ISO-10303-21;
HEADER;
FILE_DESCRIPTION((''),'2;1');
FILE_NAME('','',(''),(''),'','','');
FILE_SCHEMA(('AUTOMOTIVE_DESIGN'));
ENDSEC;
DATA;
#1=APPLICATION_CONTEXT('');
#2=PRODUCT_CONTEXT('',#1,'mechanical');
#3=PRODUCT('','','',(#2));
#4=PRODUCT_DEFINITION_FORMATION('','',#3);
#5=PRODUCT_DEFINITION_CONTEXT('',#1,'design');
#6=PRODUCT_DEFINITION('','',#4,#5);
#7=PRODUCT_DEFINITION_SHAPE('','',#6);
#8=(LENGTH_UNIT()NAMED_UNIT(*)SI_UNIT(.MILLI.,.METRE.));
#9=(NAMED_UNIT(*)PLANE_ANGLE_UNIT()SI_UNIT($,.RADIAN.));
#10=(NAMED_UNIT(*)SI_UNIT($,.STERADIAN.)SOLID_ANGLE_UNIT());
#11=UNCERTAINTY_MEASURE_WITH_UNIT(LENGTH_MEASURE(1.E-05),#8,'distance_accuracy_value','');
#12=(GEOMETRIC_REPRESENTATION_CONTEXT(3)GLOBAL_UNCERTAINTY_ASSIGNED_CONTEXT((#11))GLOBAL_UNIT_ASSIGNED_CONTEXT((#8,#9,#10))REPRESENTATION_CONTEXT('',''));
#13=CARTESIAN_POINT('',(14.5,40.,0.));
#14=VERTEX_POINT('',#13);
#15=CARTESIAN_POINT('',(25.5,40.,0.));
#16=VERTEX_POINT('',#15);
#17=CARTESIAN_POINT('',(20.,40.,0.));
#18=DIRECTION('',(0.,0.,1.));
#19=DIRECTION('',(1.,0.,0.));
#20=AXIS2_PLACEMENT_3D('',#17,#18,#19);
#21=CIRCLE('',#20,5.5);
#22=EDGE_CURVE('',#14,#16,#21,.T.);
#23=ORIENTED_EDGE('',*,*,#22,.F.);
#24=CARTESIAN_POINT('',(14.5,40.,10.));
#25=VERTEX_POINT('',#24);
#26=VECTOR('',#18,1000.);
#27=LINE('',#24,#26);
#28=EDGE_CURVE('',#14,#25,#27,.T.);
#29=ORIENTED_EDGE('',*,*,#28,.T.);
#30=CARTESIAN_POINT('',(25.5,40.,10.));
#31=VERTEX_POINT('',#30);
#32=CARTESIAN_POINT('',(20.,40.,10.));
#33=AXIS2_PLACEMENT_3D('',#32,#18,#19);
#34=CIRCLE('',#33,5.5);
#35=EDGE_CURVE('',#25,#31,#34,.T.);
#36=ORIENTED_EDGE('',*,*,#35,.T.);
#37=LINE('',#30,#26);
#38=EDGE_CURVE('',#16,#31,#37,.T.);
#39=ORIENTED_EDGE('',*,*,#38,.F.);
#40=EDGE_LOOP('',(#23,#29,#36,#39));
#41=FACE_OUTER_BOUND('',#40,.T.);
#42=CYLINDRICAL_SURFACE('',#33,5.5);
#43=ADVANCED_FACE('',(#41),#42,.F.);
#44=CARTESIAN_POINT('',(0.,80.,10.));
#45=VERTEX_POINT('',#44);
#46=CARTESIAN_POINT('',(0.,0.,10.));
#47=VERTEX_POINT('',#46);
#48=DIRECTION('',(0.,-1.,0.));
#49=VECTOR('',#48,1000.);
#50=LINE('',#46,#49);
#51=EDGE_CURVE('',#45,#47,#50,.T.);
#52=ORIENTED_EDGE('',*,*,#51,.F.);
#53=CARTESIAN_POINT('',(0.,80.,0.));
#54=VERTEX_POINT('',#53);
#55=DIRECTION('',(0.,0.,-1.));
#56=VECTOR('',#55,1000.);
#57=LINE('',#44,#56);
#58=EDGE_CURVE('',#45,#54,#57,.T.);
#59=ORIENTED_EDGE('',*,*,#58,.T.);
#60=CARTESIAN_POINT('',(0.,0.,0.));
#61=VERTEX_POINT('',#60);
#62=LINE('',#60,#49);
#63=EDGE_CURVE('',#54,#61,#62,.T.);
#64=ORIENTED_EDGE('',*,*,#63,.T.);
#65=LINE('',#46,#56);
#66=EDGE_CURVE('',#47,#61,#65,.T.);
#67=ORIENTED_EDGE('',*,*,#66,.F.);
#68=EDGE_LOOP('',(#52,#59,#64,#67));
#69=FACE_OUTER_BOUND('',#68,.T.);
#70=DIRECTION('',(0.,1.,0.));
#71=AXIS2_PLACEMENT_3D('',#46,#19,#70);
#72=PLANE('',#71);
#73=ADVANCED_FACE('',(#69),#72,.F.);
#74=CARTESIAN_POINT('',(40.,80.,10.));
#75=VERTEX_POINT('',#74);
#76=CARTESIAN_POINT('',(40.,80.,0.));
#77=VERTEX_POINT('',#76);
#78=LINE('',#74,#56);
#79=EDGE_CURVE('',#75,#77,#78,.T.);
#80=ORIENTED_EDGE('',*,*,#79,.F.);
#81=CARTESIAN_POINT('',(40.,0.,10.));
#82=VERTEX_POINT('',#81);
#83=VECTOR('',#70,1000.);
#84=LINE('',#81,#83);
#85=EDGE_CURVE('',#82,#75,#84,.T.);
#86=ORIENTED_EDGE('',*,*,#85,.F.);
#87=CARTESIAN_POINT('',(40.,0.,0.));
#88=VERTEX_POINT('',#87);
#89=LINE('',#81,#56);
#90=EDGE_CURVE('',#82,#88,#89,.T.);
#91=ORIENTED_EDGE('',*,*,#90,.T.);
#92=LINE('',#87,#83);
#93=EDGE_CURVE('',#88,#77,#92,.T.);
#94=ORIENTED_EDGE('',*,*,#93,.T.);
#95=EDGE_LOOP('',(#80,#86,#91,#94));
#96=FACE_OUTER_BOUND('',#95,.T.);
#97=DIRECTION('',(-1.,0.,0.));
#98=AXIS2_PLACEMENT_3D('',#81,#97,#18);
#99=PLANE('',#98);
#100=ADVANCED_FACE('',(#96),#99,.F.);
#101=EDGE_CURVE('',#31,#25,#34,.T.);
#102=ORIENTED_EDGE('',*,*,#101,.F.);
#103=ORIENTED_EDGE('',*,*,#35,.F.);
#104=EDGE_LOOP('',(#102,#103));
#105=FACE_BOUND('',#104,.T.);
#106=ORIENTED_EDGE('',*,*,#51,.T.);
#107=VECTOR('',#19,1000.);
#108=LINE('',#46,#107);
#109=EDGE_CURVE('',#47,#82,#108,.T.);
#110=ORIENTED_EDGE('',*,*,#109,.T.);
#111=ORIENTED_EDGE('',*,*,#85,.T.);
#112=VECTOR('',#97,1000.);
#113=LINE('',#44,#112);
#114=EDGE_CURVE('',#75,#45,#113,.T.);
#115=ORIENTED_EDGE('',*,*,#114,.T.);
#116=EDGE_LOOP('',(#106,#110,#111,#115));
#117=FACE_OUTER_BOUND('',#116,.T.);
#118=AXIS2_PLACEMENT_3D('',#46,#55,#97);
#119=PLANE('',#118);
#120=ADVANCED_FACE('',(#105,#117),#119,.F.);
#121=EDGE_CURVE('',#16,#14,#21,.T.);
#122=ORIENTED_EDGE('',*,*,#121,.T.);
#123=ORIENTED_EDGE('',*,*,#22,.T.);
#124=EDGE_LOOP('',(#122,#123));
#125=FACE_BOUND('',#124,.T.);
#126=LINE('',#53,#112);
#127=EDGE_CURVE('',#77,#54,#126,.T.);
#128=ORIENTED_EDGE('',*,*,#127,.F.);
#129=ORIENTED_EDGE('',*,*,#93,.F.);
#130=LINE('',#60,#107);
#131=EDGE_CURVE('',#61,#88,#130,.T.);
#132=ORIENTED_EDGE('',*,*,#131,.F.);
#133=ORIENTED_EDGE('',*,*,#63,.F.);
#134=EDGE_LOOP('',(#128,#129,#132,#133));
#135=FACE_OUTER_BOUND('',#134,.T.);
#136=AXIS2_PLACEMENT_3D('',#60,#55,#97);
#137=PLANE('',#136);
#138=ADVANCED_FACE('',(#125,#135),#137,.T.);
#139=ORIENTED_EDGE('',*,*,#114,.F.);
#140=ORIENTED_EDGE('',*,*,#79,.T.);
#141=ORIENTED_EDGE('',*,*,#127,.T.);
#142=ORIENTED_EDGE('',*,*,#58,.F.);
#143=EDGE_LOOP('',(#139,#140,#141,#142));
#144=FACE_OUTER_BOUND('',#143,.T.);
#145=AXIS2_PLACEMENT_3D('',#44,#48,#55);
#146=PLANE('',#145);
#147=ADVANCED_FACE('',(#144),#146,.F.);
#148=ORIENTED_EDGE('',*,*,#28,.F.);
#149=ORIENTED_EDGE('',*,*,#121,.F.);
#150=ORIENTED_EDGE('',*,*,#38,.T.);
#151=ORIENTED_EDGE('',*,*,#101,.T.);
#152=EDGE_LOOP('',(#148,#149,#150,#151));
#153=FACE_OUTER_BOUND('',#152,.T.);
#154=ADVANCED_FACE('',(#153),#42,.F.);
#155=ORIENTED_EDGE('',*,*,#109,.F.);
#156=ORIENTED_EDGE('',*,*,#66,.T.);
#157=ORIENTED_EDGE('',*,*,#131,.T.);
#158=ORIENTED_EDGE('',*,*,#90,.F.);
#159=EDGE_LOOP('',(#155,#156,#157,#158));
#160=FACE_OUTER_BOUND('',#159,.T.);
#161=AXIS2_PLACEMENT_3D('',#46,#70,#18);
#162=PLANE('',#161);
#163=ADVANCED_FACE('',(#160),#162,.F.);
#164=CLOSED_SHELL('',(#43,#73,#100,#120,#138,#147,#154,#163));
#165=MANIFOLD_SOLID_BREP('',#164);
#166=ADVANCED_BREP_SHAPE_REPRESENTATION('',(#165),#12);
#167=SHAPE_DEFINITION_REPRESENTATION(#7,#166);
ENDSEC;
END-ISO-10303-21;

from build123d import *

# Parameters (mm, degrees)
SKETCH1_W                  = 40
SKETCH1_H                  = 80
BOSS_EXTRUDE1_DEPTH        = 10
F_11_0_11_DIAMETER_HOLE1_D = 11


with BuildPart() as part:
    # Sketch1 → Boss-Extrude1 (new body)
    with BuildSketch(Plane.XY):
        with Locations((20, 40)):
            Rectangle(SKETCH1_W, SKETCH1_H)
    extrude(amount=BOSS_EXTRUDE1_DEPTH)

    # Ø11.0 (11) Diameter Hole1 (through all)
    with Locations(Plane.XY.offset(10)):
        with Locations((20, 40)):
            Hole(F_11_0_11_DIAMETER_HOLE1_D / 2)


solid = part.part
